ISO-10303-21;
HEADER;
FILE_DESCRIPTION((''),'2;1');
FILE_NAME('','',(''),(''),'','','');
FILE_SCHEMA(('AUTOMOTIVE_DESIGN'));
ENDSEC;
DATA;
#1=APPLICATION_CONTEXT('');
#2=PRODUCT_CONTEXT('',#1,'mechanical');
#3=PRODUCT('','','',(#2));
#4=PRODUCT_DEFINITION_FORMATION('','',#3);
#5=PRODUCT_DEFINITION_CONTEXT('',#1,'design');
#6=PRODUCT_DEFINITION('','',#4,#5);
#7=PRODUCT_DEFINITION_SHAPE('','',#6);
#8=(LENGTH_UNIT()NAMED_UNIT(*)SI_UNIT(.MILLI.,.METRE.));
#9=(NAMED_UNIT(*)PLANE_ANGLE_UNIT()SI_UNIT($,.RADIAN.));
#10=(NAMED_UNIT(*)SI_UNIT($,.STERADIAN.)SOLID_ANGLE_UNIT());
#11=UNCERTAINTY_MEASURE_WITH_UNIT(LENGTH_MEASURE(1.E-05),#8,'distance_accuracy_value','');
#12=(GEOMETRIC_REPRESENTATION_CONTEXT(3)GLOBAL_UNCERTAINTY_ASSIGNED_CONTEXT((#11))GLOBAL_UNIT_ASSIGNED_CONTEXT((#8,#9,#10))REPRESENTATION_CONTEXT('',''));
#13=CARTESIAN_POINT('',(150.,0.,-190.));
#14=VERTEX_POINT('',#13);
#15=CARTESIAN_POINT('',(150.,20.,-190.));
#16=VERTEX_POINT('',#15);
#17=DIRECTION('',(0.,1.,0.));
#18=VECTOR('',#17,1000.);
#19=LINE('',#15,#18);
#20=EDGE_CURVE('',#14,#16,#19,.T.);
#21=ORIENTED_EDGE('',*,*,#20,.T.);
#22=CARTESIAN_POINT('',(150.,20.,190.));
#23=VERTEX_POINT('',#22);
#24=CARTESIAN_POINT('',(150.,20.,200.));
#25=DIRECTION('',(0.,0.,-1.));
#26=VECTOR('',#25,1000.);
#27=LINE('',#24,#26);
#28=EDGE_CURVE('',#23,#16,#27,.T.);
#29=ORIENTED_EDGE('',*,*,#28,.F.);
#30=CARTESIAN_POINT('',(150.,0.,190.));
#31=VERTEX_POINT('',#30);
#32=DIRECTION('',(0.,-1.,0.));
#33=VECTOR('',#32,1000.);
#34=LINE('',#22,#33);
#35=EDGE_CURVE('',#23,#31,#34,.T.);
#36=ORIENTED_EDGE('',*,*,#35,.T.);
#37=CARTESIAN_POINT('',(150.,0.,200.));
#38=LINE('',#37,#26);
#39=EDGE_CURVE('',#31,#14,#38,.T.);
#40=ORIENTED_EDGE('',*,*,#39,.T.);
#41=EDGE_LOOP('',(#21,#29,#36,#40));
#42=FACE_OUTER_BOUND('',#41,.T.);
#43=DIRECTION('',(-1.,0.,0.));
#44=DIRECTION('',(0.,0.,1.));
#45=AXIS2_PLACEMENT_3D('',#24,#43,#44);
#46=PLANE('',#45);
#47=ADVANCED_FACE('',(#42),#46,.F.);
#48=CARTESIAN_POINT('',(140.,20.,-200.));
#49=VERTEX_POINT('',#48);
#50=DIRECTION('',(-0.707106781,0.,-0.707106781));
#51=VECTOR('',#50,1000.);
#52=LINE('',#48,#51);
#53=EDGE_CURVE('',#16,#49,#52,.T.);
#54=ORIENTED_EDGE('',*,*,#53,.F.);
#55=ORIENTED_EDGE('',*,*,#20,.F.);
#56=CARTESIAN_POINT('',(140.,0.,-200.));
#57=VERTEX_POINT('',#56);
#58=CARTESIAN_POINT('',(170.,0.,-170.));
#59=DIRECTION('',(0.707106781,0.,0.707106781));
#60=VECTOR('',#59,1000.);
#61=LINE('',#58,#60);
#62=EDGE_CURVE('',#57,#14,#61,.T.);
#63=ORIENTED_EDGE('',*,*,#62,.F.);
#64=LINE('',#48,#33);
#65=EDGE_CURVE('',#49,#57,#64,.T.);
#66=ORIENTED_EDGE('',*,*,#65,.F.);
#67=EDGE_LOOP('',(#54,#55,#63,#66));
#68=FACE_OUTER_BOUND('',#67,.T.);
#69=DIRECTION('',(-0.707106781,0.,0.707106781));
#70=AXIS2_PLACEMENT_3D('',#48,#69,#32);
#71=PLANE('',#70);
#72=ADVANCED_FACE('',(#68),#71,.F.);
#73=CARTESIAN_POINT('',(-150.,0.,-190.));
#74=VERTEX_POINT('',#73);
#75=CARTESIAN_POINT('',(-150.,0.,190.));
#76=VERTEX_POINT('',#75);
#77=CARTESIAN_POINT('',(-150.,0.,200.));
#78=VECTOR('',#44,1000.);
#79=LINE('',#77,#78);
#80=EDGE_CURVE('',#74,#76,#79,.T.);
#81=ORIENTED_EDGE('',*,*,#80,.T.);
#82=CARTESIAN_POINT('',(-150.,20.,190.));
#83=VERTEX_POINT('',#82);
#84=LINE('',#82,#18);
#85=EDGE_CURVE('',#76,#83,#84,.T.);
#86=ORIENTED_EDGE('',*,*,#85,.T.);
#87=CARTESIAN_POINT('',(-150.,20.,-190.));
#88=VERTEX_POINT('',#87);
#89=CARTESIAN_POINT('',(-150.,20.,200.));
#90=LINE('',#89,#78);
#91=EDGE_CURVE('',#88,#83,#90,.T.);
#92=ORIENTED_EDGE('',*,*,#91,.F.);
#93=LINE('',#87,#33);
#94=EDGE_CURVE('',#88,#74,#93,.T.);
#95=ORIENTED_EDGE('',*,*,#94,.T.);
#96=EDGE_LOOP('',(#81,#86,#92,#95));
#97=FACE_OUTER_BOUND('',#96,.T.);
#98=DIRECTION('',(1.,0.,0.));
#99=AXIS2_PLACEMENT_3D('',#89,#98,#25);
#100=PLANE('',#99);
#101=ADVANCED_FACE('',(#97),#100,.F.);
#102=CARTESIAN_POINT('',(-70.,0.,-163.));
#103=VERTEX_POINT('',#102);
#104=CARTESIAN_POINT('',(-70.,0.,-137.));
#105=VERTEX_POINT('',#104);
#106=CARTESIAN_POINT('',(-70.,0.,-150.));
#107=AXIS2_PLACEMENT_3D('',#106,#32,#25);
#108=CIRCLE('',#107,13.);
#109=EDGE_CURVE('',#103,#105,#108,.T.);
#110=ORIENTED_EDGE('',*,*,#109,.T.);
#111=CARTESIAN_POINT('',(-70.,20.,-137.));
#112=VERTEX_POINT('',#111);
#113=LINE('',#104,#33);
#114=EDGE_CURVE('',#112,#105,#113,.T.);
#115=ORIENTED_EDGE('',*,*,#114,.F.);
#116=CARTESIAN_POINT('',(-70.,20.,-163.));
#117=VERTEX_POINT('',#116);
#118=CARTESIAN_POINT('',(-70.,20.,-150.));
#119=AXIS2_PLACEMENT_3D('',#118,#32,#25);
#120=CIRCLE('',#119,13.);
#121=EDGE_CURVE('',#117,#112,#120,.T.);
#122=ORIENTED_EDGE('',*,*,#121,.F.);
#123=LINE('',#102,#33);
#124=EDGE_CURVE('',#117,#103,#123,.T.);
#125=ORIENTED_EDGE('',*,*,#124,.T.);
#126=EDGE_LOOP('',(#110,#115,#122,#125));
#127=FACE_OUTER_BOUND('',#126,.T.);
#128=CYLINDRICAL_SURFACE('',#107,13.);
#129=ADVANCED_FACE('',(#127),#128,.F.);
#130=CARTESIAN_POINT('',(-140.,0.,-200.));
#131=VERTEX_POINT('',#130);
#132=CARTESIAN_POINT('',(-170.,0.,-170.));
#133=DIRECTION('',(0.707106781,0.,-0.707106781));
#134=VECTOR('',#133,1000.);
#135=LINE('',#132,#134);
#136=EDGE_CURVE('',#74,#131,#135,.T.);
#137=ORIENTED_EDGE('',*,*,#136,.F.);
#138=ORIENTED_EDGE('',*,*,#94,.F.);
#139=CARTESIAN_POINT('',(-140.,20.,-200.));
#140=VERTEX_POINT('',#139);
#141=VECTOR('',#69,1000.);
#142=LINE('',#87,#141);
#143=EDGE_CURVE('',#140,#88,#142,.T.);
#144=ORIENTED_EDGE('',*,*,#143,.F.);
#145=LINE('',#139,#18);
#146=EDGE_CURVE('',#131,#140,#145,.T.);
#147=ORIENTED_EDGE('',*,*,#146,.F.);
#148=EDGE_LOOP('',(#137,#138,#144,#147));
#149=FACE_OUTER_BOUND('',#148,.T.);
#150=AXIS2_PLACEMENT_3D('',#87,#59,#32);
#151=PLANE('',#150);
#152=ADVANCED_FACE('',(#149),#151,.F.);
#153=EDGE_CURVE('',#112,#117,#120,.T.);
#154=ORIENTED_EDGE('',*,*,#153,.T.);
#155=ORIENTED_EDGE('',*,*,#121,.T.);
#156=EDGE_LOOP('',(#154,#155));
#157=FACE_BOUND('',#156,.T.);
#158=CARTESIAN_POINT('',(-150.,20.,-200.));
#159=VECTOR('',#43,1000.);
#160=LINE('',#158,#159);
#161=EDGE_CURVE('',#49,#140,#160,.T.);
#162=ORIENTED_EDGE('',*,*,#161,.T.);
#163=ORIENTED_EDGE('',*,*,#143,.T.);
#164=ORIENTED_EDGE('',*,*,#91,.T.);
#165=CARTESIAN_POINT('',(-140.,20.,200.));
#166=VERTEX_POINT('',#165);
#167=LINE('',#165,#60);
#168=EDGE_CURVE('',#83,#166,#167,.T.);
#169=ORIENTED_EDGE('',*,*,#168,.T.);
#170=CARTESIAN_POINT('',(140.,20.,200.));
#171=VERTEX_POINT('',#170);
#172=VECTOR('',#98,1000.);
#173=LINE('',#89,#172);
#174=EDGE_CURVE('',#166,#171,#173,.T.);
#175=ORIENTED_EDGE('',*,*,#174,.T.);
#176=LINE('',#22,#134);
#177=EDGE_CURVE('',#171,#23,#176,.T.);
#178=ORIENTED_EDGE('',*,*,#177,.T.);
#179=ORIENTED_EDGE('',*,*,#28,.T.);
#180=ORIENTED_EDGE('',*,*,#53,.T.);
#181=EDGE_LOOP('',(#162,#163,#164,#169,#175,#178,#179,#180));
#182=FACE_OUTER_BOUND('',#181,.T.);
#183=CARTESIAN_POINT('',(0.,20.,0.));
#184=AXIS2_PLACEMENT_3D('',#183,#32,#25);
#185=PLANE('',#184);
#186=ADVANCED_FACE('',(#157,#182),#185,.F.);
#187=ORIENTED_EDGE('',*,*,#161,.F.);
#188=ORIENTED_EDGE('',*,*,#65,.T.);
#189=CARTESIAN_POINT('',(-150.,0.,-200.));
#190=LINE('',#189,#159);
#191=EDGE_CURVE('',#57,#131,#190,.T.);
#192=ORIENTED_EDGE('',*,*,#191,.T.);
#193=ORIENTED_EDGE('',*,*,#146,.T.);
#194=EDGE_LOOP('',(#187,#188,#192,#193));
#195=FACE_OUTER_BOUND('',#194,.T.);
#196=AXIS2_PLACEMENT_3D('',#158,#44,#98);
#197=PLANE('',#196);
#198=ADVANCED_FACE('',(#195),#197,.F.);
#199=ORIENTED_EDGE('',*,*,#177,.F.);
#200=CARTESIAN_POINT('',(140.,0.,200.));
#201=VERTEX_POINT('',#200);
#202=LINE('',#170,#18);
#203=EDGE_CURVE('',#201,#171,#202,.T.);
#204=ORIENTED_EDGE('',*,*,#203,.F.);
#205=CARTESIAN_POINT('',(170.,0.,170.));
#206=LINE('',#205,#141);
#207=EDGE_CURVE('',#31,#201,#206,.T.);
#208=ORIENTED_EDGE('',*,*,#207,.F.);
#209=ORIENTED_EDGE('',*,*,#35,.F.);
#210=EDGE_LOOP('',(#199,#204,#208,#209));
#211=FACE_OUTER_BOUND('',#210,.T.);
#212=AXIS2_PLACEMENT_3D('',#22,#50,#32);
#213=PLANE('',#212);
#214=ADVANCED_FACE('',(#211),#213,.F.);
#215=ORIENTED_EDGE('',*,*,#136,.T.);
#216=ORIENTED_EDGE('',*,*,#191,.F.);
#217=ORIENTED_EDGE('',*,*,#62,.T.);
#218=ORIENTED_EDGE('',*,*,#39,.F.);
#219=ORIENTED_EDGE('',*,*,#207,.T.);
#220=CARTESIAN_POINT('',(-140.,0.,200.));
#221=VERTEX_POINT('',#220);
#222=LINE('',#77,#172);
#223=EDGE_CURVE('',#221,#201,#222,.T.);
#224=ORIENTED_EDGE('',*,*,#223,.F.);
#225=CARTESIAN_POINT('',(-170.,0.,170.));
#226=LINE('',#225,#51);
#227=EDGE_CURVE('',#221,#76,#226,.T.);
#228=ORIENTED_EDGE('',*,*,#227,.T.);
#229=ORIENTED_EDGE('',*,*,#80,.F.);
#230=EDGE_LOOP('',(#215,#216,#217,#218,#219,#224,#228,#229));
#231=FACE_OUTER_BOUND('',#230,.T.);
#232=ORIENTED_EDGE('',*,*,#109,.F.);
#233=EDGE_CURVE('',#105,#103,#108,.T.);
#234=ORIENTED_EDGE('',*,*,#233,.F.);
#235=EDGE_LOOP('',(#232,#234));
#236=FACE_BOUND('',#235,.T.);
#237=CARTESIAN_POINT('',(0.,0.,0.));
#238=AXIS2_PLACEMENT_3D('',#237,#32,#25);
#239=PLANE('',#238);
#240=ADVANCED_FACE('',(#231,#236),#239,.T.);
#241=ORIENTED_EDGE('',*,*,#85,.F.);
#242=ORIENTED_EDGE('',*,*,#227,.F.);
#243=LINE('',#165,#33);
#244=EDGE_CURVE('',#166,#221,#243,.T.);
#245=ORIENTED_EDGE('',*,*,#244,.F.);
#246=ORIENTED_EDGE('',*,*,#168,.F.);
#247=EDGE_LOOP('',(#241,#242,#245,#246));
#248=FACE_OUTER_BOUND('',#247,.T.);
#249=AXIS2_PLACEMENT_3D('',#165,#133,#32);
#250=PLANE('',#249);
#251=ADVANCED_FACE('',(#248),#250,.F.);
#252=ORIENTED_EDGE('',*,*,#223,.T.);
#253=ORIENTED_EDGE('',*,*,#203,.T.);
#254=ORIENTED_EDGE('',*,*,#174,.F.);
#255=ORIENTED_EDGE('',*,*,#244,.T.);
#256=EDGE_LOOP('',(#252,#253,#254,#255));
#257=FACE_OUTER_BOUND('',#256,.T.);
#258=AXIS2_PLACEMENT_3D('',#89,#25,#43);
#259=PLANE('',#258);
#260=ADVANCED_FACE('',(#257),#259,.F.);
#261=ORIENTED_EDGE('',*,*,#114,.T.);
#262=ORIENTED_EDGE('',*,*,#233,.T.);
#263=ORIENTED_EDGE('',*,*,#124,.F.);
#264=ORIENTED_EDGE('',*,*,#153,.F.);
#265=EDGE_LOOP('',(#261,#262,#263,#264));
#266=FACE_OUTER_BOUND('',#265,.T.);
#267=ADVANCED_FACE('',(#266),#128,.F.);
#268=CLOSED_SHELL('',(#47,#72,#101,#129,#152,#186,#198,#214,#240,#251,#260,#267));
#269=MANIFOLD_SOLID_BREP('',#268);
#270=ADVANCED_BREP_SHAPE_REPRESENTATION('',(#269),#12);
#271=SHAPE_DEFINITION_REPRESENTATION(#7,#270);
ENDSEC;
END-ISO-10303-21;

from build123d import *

# Parameters (mm, degrees)
SKETCH_1_W          = 300
SKETCH_1_H          = 400
EXTRUDE_1_DEPTH     = 20
CHAMFER_1_SIZE      = 10
HOLE_WIZARD_M24_1_D = 26


with BuildPart() as part:
    # 草图1 → 凸台-拉伸1 (new body)
    with BuildSketch(Plane(origin=(0, 0, 0), x_dir=(1, 0, 0), z_dir=(0, 1, 0))):
        Rectangle(SKETCH_1_W, SKETCH_1_H)
    extrude(amount=EXTRUDE_1_DEPTH)

    # 倒角1
    chamfer_1_edges = [part.edges().sort_by_distance(p)[0] for p in [
        (150, 10, 200),
        (-150, 10, 200),
        (-150, 10, -200),
        (150, 10, -200),
    ]]
    chamfer(chamfer_1_edges, length=CHAMFER_1_SIZE)

    # M24 间隙孔1 (through all)
    with Locations(Plane(origin=(0, 0, 0), x_dir=(-1, 0, 0), z_dir=(0, -1, 0))):
        with Locations((70, 150)):
            Hole(HOLE_WIZARD_M24_1_D / 2)


solid = part.part
